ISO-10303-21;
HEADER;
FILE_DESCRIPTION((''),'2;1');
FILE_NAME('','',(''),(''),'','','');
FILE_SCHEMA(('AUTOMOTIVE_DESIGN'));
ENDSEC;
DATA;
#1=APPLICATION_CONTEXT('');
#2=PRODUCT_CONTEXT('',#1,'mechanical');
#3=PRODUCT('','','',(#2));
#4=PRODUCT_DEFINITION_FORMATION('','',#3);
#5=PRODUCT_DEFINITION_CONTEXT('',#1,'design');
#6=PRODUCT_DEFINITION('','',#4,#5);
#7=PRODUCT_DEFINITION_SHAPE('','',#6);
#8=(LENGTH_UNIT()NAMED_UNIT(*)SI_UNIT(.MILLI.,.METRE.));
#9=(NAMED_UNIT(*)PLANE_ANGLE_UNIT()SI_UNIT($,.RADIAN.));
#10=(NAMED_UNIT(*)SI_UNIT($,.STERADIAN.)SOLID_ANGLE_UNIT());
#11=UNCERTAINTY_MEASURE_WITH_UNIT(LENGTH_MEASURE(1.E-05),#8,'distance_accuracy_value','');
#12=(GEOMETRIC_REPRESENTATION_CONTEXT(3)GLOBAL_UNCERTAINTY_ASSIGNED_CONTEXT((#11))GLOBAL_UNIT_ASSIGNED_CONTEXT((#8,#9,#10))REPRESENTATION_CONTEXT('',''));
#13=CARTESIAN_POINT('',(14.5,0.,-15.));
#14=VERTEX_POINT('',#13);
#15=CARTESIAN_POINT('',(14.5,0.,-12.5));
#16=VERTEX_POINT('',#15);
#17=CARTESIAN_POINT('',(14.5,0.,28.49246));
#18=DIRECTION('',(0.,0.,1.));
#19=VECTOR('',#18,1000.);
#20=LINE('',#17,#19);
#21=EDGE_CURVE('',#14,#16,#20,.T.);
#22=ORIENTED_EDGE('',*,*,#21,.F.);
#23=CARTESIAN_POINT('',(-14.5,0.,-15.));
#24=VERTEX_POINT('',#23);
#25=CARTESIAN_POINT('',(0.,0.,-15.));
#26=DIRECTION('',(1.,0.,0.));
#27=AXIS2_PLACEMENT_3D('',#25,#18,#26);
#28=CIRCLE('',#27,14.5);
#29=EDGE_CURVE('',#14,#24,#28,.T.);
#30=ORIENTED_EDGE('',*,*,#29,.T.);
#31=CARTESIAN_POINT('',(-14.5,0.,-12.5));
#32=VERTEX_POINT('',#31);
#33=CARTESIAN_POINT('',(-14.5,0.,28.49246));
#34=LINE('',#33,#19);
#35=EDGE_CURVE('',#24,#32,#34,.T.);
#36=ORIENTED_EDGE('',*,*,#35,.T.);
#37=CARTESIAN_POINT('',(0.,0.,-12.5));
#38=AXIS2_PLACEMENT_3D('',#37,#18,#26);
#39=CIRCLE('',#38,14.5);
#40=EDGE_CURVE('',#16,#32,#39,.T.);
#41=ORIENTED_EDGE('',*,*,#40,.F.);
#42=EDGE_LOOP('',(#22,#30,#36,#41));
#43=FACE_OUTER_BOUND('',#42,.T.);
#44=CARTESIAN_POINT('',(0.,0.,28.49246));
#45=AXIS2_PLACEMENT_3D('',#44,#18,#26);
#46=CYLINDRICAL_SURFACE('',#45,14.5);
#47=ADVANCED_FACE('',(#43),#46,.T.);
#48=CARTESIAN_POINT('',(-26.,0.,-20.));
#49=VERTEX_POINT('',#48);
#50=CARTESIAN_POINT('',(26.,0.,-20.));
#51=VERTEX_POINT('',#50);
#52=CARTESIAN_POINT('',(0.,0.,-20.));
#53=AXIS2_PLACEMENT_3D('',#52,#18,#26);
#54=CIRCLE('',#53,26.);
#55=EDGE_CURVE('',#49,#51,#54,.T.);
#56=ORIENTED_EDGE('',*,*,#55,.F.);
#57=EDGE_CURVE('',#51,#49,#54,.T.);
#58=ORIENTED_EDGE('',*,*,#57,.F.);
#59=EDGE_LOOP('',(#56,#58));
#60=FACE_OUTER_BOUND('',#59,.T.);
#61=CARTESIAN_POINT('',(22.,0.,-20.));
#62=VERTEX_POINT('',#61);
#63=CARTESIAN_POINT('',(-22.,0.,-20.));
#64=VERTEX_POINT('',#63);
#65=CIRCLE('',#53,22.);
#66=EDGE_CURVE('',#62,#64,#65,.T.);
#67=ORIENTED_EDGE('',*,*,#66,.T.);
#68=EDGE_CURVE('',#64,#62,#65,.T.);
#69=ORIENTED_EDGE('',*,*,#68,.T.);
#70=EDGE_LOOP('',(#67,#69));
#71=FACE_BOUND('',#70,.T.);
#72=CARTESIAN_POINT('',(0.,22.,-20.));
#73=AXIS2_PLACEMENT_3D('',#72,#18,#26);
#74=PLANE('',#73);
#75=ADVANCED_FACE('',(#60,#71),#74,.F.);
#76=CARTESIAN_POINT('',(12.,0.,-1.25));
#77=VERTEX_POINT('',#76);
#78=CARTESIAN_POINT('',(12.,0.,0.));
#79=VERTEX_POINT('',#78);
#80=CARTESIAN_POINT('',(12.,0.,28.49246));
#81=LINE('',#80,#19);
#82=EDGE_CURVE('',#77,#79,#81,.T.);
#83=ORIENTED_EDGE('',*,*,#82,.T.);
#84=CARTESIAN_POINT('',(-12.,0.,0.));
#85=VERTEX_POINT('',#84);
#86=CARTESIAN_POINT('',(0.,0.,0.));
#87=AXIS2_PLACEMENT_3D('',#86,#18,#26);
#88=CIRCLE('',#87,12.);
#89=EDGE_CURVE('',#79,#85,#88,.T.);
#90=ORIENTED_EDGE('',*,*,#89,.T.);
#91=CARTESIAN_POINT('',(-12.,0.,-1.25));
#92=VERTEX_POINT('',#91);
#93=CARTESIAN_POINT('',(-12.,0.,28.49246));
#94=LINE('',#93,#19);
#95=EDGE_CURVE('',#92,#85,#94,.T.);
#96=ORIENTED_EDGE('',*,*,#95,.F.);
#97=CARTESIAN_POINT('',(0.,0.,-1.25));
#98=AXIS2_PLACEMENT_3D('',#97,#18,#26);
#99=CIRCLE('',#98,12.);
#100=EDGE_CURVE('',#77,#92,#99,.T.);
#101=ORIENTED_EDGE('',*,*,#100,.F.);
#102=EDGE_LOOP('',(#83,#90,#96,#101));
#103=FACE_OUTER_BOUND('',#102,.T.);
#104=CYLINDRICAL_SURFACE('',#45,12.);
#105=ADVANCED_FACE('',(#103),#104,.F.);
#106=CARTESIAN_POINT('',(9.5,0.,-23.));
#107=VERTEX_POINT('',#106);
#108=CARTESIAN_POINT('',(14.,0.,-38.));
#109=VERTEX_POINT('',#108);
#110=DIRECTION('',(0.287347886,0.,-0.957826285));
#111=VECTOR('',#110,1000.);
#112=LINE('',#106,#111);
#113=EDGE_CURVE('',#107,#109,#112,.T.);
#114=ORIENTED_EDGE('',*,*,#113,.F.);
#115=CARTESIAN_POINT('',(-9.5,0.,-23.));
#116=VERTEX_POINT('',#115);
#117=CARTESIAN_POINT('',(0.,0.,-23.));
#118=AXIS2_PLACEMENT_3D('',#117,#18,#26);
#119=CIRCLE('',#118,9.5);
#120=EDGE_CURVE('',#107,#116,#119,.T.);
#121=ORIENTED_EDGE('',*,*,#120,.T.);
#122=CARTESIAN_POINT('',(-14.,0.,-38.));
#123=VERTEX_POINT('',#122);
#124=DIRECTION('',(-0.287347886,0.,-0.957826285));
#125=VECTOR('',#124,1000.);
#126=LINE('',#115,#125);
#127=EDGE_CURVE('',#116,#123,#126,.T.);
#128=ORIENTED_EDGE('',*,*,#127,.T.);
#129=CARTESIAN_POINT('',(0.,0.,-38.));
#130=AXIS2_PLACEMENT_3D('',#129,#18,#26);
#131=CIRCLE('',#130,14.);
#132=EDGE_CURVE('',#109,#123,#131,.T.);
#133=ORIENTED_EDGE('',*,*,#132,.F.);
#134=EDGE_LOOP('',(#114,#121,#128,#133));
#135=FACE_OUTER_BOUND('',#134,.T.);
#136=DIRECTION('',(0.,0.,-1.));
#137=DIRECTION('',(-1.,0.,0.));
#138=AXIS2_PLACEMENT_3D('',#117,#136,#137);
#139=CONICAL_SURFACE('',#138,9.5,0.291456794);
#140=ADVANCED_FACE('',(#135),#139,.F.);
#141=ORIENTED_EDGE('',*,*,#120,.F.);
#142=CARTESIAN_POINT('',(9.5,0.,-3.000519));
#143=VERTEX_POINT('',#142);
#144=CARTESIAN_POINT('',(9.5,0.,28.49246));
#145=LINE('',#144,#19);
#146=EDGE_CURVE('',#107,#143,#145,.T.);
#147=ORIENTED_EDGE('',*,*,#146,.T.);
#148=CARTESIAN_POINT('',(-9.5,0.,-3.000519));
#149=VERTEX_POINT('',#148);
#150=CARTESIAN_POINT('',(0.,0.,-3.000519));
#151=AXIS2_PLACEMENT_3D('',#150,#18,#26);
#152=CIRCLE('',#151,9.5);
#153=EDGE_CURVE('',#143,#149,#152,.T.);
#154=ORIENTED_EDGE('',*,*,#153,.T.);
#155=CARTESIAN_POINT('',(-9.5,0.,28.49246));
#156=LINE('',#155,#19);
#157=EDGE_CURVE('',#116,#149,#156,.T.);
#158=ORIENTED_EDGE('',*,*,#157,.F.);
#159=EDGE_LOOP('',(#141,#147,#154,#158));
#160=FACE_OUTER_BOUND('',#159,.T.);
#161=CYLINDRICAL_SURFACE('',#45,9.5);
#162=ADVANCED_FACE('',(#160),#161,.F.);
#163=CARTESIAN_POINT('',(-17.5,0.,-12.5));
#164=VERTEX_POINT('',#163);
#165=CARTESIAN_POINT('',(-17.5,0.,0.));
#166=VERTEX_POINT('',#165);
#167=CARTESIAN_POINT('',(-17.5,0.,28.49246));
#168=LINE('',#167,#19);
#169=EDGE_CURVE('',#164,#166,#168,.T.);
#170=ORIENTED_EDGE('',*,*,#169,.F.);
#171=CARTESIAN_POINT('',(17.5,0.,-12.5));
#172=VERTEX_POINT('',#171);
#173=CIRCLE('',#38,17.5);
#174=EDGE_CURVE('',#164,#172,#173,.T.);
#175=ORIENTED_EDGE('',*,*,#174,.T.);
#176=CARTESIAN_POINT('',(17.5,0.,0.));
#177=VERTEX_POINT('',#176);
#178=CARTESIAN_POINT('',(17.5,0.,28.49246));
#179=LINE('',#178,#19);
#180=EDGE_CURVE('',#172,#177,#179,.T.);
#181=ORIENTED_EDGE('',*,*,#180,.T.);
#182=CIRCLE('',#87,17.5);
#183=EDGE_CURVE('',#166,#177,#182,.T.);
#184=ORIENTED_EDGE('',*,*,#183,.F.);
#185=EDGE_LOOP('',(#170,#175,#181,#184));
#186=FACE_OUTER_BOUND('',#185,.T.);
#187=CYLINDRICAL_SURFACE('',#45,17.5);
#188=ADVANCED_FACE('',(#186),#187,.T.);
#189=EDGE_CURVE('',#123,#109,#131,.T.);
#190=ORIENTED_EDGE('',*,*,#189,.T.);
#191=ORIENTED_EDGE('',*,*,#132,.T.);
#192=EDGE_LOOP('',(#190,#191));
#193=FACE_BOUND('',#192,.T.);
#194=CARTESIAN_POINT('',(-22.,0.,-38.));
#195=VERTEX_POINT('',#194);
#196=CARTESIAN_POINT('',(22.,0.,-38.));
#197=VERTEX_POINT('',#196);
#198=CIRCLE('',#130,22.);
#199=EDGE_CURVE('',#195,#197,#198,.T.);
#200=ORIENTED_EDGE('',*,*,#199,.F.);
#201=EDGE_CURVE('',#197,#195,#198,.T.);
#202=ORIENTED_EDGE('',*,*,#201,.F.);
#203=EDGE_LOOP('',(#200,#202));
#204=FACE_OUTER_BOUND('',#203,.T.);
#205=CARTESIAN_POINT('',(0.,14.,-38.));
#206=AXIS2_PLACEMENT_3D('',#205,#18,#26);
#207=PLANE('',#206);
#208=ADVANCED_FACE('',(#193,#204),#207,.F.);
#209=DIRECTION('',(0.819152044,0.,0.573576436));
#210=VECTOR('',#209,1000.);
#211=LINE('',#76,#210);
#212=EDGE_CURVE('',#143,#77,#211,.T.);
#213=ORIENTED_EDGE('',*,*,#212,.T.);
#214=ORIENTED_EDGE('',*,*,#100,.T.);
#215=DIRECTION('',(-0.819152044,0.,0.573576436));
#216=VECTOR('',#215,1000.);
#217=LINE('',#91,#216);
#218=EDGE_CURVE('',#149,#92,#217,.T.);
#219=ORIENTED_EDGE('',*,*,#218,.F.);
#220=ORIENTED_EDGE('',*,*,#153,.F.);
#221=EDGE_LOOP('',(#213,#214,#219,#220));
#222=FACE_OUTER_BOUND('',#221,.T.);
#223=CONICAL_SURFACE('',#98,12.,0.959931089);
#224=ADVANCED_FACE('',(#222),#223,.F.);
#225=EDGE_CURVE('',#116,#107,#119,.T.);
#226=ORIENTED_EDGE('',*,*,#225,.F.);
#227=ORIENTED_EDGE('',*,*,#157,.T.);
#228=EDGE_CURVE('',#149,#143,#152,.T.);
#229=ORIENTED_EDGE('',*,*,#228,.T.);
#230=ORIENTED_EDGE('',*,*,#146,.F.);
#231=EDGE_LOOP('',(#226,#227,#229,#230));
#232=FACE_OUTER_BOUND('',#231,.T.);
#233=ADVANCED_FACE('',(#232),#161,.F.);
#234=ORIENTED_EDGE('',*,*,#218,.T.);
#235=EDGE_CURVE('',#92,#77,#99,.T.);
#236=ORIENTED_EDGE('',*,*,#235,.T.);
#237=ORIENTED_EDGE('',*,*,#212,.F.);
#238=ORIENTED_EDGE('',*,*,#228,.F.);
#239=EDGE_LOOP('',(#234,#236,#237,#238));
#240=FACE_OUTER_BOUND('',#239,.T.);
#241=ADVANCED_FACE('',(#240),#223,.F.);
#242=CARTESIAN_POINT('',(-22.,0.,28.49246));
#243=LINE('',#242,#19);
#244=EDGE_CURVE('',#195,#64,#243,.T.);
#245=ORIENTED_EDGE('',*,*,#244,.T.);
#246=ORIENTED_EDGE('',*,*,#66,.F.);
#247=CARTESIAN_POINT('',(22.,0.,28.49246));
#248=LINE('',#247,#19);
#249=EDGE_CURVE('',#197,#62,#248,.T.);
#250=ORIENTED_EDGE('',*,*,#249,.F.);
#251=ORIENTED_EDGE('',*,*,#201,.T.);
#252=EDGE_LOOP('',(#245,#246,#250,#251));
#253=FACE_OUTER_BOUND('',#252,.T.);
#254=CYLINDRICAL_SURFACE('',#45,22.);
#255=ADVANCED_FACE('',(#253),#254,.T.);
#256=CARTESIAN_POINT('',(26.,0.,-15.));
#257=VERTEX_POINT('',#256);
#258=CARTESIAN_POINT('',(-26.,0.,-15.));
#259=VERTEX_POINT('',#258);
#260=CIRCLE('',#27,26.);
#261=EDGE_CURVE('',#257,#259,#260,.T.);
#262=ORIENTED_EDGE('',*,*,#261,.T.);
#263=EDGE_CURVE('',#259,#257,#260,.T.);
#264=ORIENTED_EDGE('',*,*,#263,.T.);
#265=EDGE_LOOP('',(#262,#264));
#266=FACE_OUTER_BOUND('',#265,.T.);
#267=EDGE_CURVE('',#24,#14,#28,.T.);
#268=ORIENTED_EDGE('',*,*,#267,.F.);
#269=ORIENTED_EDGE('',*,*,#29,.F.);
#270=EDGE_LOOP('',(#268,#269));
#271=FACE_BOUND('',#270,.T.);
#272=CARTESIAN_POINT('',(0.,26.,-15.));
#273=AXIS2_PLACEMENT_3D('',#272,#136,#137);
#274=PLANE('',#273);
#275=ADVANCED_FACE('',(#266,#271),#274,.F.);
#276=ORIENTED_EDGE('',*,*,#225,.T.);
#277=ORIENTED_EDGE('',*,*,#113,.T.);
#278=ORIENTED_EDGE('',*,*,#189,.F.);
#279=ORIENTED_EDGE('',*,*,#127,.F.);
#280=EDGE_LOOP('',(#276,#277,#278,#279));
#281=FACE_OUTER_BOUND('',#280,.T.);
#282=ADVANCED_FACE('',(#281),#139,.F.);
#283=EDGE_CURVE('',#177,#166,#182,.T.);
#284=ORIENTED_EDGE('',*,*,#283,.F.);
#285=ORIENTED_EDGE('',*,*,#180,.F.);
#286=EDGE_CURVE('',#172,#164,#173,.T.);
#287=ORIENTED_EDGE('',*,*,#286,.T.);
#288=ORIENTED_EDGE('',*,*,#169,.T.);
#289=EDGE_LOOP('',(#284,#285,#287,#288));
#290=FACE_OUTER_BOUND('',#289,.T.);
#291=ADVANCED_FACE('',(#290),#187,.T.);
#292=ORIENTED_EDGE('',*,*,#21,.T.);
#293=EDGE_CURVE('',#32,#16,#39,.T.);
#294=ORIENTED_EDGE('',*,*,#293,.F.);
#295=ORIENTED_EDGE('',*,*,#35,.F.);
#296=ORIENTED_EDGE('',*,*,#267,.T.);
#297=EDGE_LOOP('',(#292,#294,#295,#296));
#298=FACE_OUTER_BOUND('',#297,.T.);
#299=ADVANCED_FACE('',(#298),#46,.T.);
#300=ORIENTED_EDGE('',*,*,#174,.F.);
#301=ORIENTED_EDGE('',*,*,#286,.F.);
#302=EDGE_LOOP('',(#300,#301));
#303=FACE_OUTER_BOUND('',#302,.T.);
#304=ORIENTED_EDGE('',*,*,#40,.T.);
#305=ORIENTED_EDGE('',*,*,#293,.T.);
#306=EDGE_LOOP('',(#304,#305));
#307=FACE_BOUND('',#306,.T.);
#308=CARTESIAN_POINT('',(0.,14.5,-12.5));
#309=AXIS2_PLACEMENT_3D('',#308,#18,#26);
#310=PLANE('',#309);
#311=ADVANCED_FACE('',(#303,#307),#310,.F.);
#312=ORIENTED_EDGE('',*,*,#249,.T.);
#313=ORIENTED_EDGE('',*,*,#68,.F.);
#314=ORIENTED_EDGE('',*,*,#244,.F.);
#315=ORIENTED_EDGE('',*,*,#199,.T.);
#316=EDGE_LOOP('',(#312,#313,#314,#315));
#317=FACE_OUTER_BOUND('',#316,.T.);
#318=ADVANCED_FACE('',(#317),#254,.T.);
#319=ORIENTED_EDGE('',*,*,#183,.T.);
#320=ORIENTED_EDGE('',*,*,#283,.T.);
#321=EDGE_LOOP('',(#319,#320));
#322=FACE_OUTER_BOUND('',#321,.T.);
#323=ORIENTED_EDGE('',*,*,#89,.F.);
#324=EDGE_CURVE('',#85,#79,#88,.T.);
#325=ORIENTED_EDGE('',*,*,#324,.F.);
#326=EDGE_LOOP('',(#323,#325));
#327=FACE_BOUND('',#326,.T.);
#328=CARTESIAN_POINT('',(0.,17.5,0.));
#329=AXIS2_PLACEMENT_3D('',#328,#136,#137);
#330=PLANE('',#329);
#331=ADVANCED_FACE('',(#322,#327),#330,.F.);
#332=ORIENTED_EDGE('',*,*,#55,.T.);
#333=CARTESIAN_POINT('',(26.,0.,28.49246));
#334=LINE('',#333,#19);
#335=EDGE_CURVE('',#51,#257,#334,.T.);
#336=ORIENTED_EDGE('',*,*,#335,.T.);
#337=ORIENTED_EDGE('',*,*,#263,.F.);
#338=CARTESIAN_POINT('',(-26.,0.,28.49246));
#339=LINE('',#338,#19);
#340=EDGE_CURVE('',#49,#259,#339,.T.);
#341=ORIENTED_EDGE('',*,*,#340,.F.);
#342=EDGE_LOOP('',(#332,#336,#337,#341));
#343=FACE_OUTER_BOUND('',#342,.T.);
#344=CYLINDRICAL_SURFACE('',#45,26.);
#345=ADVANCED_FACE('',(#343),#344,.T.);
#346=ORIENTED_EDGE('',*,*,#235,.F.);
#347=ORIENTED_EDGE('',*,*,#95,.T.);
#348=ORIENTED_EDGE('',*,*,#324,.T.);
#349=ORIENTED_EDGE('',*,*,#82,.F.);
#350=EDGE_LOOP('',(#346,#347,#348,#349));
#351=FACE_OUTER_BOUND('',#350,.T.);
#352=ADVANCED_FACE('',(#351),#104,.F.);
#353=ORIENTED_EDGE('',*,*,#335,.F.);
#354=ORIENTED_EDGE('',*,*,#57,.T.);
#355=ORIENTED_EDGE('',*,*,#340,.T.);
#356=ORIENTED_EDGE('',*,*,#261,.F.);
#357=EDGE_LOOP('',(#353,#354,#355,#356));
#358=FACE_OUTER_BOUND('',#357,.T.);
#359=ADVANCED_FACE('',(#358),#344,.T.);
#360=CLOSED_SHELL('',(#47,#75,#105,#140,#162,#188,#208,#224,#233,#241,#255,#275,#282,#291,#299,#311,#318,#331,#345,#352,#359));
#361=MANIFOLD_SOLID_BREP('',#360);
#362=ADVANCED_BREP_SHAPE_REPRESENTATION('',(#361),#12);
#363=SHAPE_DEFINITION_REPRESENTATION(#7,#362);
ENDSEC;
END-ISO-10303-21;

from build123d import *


with BuildPart() as part:
    # Sketch2 → Revolve1 (revolve)
    with BuildSketch(Plane(origin=(0, 0, 0), x_dir=(0, 0, -1), z_dir=(1, 0, 0)), mode=Mode.PRIVATE) as revolve1_sk:
        Polygon((0, 17.5), (0, 12), (1.25, 12), (3.000518846, 9.5), (23, 9.5), (38, 14), (38, 22), (20, 22), (20, 26), (15, 26), (15, 14.5), (12.5, 14.5), (12.5, 17.5), align=None)
    revolve(revolve1_sk.sketch.rotate(Axis((0, 0, 28.492460363), (0, 0, -1)), 90), axis=Axis((0, 0, 28.492460363), (0, 0, -1)))


solid = part.part
